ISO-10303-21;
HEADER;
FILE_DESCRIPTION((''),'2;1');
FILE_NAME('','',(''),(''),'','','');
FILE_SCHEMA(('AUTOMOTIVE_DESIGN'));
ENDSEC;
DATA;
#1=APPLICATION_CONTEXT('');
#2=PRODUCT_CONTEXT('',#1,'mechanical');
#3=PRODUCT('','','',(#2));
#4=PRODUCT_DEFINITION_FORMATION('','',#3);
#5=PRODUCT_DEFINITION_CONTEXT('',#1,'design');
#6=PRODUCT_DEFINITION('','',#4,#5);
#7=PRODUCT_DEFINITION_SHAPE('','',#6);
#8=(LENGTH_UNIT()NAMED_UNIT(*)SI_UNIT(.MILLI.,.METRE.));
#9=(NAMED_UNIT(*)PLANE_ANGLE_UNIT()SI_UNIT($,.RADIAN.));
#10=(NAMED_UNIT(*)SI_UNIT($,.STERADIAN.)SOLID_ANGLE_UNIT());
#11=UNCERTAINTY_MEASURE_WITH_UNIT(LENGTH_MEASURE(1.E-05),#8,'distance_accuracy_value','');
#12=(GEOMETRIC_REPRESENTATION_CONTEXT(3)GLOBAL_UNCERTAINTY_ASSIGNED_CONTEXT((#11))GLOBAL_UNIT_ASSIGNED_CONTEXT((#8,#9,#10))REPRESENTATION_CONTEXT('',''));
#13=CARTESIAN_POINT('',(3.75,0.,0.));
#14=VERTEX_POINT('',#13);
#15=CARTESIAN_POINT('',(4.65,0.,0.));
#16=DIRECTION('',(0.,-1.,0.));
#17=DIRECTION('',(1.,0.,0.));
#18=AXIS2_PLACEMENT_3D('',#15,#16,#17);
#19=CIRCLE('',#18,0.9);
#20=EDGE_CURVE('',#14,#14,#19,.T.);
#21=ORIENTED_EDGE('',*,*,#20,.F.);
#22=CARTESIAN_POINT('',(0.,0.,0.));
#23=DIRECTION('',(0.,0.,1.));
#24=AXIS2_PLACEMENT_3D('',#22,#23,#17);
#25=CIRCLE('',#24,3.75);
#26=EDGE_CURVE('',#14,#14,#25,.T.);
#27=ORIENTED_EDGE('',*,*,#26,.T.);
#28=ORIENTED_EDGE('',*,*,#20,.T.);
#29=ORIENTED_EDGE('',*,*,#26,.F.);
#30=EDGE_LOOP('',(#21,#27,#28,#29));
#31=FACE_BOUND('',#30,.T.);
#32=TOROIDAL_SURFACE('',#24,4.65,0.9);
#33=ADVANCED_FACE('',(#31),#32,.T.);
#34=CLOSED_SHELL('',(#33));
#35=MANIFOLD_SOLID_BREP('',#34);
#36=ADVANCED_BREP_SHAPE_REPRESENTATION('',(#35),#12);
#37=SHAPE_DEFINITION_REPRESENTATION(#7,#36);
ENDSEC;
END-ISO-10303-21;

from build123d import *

# Parameters (mm, degrees)
SKETCH2_R = 0.9


with BuildPart() as part:
    # Sweep1: sweep along a path in Sketch1
    with BuildLine(Plane.XY) as sweep1_path:
        CenterArc((0, 0), 3.75, 0, 360)
    # Sketch2 → Sweep1 (sweep)
    with BuildSketch(Plane(origin=(0, 0, 0), x_dir=(1, 0, 0), z_dir=(0, 1, 0))):
        with Locations((-4.65, 0)):
            Circle(SKETCH2_R)
    sweep(path=sweep1_path.line)


solid = part.part
